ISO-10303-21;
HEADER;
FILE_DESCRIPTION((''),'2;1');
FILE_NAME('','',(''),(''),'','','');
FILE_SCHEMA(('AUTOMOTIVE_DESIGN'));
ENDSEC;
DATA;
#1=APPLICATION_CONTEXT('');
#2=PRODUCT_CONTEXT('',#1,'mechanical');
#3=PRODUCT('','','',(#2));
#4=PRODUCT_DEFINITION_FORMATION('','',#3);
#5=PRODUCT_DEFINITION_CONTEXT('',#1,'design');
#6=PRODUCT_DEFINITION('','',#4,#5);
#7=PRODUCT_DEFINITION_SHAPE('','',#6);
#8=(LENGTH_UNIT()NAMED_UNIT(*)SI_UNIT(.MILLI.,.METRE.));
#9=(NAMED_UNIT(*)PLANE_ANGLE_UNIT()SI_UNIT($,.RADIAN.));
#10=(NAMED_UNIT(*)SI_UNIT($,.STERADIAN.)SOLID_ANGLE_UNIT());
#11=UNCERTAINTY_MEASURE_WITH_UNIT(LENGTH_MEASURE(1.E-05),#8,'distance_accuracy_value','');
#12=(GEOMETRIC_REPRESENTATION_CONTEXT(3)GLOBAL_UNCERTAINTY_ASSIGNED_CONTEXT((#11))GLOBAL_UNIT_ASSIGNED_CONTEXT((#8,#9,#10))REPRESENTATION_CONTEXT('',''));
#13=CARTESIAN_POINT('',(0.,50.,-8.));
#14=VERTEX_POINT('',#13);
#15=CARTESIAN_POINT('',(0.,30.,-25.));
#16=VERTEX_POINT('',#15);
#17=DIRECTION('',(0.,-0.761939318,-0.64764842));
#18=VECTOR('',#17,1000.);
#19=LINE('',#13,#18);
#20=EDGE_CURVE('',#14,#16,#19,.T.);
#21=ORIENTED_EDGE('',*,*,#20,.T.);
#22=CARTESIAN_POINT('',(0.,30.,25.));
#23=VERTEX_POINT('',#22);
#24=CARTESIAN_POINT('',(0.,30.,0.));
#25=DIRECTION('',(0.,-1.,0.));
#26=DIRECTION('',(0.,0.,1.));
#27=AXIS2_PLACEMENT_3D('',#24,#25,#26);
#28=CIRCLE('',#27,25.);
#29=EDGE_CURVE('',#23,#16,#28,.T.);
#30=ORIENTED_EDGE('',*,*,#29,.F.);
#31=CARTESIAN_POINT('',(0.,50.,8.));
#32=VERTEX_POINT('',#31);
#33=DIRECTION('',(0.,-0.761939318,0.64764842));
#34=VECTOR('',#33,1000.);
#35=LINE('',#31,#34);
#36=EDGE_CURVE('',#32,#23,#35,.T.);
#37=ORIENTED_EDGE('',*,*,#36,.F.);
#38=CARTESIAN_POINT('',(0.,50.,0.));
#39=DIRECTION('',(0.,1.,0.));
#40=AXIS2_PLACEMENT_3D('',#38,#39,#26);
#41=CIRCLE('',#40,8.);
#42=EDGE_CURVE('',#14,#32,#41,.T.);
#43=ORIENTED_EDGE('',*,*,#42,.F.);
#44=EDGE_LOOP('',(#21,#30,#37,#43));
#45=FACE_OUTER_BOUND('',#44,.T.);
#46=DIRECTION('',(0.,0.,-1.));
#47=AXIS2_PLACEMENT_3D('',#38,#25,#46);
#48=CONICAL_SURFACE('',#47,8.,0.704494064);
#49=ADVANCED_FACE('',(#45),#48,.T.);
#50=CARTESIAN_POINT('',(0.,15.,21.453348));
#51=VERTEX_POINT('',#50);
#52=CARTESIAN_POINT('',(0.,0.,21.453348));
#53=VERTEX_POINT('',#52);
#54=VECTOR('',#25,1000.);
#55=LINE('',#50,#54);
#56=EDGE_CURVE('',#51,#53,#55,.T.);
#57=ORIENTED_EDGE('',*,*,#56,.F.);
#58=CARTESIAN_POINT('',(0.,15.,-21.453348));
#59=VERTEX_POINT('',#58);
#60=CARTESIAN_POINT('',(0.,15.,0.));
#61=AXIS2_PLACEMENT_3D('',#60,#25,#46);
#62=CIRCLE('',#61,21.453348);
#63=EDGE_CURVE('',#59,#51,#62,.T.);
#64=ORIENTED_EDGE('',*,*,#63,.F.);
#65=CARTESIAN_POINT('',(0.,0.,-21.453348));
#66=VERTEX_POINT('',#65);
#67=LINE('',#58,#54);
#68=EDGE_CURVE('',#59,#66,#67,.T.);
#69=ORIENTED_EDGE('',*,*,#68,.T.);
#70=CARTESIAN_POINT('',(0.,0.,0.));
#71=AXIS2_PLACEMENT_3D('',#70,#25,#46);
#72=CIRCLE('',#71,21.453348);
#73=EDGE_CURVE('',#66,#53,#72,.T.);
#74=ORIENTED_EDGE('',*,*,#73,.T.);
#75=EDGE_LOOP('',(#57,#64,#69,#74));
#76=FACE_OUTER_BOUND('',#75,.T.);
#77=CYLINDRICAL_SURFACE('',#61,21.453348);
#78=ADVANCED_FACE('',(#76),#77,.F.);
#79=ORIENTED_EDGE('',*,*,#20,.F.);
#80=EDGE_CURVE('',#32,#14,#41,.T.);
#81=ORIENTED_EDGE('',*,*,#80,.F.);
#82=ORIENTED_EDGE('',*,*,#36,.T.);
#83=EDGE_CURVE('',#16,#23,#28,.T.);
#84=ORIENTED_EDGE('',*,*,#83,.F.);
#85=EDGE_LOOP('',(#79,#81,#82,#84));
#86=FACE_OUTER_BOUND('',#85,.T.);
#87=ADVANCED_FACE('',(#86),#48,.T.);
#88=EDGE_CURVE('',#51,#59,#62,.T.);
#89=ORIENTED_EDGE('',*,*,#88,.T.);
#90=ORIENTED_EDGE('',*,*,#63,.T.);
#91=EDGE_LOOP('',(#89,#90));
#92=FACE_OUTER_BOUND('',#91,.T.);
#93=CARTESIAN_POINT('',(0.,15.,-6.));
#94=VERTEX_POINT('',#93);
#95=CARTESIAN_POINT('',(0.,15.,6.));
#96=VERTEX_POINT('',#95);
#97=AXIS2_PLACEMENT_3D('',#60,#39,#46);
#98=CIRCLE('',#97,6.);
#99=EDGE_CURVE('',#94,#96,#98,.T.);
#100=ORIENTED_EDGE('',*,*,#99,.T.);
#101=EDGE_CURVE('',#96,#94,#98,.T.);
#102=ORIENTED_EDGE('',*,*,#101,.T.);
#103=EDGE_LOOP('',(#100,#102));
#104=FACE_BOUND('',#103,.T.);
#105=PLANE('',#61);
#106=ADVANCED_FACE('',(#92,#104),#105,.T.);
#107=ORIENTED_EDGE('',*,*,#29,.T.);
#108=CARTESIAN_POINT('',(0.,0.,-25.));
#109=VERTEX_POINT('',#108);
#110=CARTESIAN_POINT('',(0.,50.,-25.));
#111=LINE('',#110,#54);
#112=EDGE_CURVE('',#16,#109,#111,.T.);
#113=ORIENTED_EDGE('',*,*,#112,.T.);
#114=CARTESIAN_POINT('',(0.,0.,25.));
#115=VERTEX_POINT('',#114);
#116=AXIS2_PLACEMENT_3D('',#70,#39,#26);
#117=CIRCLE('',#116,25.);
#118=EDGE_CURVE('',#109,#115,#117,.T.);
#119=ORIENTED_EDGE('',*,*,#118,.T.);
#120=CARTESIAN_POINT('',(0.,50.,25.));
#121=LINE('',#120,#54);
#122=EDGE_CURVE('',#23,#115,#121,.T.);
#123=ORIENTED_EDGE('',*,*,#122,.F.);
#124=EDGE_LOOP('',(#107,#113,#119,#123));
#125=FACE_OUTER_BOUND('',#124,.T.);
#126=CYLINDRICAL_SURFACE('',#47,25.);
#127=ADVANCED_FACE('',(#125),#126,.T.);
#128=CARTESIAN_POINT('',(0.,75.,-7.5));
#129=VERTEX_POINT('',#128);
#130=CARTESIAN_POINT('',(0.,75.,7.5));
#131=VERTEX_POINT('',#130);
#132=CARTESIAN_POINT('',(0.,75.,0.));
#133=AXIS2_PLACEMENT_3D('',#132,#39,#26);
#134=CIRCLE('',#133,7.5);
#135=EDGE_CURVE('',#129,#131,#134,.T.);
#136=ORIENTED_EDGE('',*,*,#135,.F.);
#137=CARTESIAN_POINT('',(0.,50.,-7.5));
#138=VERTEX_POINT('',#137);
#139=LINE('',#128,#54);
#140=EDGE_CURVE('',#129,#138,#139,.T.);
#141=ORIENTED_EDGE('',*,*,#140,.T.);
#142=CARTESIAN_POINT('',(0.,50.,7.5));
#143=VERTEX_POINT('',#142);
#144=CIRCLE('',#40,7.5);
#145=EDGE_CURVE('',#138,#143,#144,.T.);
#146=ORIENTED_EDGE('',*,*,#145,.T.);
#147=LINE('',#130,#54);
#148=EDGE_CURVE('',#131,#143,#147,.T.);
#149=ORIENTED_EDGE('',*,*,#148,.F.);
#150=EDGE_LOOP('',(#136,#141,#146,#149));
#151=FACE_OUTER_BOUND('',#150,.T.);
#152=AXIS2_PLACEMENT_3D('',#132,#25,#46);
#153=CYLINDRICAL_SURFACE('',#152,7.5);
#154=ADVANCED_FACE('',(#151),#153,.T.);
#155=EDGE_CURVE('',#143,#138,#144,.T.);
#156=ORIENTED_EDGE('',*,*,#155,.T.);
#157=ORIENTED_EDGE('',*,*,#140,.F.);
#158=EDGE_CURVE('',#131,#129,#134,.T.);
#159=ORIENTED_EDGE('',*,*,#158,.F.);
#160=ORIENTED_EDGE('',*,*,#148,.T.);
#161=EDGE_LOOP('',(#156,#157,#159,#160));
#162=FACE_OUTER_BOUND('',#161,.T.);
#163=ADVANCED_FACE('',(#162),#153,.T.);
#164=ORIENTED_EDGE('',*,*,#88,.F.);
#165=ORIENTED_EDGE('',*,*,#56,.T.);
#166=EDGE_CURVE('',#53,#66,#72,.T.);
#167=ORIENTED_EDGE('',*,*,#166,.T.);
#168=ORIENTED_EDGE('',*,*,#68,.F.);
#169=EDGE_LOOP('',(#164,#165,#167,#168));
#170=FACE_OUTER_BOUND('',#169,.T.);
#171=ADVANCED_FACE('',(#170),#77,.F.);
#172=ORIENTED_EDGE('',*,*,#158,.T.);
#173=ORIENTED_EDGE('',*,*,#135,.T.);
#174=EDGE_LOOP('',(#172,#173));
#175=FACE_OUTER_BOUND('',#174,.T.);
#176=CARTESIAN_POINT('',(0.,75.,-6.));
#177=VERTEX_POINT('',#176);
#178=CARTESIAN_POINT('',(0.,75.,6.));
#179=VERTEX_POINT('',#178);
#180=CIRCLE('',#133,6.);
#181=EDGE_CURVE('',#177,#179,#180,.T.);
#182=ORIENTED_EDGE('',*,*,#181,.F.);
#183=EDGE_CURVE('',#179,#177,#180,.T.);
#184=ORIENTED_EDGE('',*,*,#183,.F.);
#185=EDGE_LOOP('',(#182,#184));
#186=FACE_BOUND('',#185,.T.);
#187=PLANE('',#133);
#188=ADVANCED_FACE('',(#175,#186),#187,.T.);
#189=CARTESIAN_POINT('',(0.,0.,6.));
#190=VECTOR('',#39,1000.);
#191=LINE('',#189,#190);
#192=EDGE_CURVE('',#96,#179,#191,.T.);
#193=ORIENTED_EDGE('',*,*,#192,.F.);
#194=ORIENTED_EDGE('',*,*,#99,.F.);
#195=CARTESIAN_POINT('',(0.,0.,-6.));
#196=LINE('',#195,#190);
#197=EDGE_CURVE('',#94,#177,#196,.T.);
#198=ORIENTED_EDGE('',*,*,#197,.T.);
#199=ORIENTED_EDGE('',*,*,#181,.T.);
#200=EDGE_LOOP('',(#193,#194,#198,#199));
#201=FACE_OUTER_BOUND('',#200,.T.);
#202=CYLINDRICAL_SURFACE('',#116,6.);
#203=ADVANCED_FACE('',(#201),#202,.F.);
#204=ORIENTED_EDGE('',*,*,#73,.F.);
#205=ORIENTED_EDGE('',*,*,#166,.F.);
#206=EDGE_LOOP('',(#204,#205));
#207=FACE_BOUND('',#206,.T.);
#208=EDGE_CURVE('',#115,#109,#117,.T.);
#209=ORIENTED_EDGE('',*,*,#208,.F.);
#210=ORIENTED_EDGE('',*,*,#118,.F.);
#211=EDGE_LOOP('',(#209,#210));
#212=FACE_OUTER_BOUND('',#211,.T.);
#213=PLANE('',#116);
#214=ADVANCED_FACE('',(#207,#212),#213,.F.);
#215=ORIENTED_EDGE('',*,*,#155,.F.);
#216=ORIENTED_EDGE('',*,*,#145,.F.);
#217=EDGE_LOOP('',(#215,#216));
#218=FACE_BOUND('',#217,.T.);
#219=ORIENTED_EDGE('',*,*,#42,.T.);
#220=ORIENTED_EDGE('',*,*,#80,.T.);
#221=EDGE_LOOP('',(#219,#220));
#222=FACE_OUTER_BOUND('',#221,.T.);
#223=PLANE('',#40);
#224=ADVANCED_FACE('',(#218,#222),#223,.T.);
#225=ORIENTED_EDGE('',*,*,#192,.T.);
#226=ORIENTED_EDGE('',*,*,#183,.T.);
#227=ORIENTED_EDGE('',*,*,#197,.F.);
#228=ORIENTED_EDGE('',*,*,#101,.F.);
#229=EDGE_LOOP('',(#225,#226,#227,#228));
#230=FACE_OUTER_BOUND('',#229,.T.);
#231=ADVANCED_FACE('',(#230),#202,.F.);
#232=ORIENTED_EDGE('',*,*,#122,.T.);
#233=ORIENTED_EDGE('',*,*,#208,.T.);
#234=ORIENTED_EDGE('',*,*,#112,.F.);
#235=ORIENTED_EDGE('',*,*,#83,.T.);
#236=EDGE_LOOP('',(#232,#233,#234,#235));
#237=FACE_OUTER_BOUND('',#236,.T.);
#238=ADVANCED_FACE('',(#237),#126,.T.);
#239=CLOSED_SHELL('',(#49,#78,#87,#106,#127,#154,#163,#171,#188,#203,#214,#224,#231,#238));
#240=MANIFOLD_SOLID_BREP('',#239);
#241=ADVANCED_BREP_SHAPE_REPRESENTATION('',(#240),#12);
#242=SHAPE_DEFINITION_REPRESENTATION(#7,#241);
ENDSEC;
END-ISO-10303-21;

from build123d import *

# Parameters (mm, degrees)
SKETCH1_R           = 25
BOSS_EXTRUDE1_DEPTH = 50
SKETCH2_R           = 7.5
BOSS_EXTRUDE2_DEPTH = 25
CHAMFER1_SIZE       = 20
CHAMFER1_SIZE2      = 17
SKETCH3_R           = 6
CUT_EXTRUDE1_DEPTH  = 83.915619759
SKETCH4_R           = 21.453348456
CUT_EXTRUDE2_DEPTH  = 15


with BuildPart() as part:
    # Sketch1 → Boss-Extrude1 (new body)
    with BuildSketch(Plane(origin=(0, 0, 0), x_dir=(1, 0, 0), z_dir=(0, 1, 0))):
        with Locations(Location((0, 0, 0), (0, 0, 270))):
            Circle(SKETCH1_R)
    extrude(amount=BOSS_EXTRUDE1_DEPTH)

    # Sketch2 → Boss-Extrude2 (add)
    with BuildSketch(Plane(origin=(0, 50, 0), x_dir=(1, 0, 0), z_dir=(0, 1, 0))):
        with Locations(Location((0, 0, 0), (0, 0, 270))):
            Circle(SKETCH2_R)
    extrude(amount=BOSS_EXTRUDE2_DEPTH)

    # Chamfer1
    chamfer1_edges = [part.edges().sort_by_distance(p)[0] for p in [
        (0, 50, -25),
    ]]
    chamfer1_side = [part.faces().sort_by_distance(p)[0] for p in [
        (0, 25, -25),
    ]]
    chamfer(chamfer1_edges, length=CHAMFER1_SIZE, length2=CHAMFER1_SIZE2, reference=chamfer1_side[0])

    # Sketch3 → Cut-Extrude1 (cut, through all)
    with BuildSketch(Plane(origin=(0, 75, 0), x_dir=(1, 0, 0), z_dir=(0, 1, 0))):
        with Locations(Location((0, 0, 0), (0, 0, 270))):
            Circle(SKETCH3_R)
    extrude(amount=-CUT_EXTRUDE1_DEPTH, mode=Mode.SUBTRACT)

    # Sketch4 → Cut-Extrude2 (cut)
    with BuildSketch(Plane.XZ):
        with Locations(Location((0, 0, 0), (0, 0, 270))):
            Circle(SKETCH4_R)
    extrude(amount=-CUT_EXTRUDE2_DEPTH, mode=Mode.SUBTRACT)


solid = part.part
